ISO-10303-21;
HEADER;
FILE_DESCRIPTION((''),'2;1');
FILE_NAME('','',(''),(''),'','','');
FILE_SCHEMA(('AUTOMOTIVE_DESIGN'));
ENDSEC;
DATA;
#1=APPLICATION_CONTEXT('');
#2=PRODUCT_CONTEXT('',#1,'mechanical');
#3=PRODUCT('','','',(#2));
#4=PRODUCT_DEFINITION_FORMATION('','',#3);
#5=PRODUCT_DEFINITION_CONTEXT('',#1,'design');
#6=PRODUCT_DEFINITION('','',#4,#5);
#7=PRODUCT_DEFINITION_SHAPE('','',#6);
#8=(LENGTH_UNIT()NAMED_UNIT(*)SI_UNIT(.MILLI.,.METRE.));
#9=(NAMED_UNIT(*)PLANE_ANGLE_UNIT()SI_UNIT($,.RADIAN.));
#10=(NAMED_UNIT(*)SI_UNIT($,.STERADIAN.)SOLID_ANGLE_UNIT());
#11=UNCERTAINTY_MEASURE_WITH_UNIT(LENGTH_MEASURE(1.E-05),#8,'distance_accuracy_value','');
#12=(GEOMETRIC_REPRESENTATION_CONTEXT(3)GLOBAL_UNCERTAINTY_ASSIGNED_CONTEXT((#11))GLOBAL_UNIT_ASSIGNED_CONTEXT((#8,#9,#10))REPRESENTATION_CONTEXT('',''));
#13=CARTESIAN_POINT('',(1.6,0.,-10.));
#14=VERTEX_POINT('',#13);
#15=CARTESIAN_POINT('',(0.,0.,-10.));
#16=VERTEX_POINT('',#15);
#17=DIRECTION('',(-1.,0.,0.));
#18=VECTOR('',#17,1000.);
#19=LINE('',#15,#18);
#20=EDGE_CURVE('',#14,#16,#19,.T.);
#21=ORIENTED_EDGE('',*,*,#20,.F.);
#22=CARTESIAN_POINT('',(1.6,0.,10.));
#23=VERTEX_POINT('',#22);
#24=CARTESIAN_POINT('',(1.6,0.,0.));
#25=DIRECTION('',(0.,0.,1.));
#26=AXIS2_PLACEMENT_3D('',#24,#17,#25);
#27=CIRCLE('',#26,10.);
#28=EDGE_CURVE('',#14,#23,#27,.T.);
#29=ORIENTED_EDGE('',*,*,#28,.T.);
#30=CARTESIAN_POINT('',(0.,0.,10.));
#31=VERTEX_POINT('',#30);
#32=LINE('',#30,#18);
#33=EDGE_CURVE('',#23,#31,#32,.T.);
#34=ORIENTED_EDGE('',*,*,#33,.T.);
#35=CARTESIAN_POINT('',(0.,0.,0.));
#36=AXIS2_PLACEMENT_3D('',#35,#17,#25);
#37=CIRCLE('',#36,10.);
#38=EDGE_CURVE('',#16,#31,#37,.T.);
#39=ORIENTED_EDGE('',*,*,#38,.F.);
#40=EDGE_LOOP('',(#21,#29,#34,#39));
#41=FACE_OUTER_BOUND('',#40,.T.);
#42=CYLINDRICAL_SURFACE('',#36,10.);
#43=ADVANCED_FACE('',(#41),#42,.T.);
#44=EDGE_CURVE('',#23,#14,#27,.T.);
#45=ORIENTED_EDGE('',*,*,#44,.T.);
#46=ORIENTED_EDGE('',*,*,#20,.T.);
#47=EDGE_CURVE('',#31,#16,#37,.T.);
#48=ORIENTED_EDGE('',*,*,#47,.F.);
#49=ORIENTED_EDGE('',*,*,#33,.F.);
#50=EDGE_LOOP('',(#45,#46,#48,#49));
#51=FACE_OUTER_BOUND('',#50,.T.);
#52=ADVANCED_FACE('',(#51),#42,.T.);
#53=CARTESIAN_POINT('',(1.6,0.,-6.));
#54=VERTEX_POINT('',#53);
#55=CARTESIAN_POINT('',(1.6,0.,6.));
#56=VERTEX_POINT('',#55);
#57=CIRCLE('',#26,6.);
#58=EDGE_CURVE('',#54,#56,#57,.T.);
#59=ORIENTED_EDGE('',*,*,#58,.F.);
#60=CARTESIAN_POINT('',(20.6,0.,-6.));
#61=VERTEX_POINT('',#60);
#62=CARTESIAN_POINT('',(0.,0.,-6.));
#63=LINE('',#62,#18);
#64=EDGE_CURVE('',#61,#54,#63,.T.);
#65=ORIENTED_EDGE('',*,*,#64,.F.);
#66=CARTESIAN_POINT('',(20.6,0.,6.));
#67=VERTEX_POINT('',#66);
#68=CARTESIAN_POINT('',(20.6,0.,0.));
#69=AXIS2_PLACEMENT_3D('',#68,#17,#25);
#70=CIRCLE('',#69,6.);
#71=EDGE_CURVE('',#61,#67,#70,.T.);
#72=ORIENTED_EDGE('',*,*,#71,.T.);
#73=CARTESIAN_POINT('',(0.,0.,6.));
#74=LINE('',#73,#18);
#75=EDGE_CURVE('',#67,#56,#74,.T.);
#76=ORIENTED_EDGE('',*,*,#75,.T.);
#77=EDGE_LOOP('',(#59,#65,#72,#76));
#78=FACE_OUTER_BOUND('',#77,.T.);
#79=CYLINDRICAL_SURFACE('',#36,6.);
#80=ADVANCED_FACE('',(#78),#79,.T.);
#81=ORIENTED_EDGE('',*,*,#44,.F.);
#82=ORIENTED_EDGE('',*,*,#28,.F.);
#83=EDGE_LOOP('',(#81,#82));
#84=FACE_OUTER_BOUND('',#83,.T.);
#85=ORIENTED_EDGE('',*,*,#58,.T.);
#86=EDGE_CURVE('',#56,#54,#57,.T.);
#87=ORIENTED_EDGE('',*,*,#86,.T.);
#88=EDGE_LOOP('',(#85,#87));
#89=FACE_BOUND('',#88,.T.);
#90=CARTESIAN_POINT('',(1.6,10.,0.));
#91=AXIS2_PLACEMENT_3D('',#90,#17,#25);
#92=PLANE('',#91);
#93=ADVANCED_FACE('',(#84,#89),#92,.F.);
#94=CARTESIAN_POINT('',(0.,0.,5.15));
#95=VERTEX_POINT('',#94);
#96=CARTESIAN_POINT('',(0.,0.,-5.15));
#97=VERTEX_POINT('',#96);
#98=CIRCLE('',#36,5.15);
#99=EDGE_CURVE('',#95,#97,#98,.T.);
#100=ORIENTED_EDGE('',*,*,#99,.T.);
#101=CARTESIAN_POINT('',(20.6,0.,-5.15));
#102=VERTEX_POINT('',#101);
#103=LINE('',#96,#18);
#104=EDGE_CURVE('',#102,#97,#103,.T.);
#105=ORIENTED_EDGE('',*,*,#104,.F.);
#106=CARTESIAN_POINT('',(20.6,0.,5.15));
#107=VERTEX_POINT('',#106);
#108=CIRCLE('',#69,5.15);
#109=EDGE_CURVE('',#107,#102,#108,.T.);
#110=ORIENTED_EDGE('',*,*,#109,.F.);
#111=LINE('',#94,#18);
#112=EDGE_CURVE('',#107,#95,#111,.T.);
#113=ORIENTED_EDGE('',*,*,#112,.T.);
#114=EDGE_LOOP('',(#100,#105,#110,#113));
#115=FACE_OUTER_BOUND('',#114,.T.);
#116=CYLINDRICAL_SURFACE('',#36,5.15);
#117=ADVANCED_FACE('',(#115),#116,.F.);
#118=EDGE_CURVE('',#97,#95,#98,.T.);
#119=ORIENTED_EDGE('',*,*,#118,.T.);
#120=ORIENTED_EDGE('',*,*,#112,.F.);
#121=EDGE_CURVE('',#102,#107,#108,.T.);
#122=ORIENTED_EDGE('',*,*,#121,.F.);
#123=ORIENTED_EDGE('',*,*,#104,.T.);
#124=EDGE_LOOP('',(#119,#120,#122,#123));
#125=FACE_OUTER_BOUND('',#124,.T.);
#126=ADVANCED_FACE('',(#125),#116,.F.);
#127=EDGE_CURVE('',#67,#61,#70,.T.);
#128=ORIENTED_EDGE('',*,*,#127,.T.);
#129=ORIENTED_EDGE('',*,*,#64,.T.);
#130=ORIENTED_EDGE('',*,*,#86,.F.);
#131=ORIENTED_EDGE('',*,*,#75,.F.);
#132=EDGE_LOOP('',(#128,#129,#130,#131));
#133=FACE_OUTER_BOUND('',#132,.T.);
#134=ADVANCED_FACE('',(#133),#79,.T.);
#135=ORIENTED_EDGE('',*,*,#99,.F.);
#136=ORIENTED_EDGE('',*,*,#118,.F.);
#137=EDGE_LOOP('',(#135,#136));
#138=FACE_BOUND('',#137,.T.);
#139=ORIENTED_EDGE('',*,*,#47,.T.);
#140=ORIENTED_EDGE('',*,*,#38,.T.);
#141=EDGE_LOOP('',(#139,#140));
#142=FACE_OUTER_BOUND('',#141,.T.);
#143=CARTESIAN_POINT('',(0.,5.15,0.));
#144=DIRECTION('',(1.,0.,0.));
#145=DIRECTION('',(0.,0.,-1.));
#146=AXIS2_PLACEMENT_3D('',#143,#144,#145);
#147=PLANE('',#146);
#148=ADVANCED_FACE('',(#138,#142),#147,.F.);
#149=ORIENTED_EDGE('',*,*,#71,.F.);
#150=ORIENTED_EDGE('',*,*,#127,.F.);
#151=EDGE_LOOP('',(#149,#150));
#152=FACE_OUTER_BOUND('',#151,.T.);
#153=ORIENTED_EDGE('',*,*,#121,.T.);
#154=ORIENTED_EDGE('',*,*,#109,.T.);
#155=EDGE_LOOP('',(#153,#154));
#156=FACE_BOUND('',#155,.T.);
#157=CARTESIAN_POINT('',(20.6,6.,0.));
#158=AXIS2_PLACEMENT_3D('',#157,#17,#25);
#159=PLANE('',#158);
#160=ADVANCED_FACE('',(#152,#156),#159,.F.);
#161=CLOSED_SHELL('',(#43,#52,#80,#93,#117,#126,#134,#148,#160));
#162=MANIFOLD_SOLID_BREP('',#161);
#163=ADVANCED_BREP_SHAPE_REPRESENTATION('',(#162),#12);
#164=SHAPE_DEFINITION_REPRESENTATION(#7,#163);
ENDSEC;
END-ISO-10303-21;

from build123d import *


with BuildPart() as part:
    # 草图1 → 旋转1 (revolve)
    with BuildSketch(Plane.XY, mode=Mode.PRIVATE) as revolve_1_sk:
        Polygon((0, 5.15), (0, 10), (1.6, 10), (1.6, 6), (20.6, 6), (20.6, 5.15), align=None)
    revolve(revolve_1_sk.sketch.rotate(Axis((0, 0, 0), (1, 0, 0)), 90), axis=Axis((0, 0, 0), (1, 0, 0)))


solid = part.part
